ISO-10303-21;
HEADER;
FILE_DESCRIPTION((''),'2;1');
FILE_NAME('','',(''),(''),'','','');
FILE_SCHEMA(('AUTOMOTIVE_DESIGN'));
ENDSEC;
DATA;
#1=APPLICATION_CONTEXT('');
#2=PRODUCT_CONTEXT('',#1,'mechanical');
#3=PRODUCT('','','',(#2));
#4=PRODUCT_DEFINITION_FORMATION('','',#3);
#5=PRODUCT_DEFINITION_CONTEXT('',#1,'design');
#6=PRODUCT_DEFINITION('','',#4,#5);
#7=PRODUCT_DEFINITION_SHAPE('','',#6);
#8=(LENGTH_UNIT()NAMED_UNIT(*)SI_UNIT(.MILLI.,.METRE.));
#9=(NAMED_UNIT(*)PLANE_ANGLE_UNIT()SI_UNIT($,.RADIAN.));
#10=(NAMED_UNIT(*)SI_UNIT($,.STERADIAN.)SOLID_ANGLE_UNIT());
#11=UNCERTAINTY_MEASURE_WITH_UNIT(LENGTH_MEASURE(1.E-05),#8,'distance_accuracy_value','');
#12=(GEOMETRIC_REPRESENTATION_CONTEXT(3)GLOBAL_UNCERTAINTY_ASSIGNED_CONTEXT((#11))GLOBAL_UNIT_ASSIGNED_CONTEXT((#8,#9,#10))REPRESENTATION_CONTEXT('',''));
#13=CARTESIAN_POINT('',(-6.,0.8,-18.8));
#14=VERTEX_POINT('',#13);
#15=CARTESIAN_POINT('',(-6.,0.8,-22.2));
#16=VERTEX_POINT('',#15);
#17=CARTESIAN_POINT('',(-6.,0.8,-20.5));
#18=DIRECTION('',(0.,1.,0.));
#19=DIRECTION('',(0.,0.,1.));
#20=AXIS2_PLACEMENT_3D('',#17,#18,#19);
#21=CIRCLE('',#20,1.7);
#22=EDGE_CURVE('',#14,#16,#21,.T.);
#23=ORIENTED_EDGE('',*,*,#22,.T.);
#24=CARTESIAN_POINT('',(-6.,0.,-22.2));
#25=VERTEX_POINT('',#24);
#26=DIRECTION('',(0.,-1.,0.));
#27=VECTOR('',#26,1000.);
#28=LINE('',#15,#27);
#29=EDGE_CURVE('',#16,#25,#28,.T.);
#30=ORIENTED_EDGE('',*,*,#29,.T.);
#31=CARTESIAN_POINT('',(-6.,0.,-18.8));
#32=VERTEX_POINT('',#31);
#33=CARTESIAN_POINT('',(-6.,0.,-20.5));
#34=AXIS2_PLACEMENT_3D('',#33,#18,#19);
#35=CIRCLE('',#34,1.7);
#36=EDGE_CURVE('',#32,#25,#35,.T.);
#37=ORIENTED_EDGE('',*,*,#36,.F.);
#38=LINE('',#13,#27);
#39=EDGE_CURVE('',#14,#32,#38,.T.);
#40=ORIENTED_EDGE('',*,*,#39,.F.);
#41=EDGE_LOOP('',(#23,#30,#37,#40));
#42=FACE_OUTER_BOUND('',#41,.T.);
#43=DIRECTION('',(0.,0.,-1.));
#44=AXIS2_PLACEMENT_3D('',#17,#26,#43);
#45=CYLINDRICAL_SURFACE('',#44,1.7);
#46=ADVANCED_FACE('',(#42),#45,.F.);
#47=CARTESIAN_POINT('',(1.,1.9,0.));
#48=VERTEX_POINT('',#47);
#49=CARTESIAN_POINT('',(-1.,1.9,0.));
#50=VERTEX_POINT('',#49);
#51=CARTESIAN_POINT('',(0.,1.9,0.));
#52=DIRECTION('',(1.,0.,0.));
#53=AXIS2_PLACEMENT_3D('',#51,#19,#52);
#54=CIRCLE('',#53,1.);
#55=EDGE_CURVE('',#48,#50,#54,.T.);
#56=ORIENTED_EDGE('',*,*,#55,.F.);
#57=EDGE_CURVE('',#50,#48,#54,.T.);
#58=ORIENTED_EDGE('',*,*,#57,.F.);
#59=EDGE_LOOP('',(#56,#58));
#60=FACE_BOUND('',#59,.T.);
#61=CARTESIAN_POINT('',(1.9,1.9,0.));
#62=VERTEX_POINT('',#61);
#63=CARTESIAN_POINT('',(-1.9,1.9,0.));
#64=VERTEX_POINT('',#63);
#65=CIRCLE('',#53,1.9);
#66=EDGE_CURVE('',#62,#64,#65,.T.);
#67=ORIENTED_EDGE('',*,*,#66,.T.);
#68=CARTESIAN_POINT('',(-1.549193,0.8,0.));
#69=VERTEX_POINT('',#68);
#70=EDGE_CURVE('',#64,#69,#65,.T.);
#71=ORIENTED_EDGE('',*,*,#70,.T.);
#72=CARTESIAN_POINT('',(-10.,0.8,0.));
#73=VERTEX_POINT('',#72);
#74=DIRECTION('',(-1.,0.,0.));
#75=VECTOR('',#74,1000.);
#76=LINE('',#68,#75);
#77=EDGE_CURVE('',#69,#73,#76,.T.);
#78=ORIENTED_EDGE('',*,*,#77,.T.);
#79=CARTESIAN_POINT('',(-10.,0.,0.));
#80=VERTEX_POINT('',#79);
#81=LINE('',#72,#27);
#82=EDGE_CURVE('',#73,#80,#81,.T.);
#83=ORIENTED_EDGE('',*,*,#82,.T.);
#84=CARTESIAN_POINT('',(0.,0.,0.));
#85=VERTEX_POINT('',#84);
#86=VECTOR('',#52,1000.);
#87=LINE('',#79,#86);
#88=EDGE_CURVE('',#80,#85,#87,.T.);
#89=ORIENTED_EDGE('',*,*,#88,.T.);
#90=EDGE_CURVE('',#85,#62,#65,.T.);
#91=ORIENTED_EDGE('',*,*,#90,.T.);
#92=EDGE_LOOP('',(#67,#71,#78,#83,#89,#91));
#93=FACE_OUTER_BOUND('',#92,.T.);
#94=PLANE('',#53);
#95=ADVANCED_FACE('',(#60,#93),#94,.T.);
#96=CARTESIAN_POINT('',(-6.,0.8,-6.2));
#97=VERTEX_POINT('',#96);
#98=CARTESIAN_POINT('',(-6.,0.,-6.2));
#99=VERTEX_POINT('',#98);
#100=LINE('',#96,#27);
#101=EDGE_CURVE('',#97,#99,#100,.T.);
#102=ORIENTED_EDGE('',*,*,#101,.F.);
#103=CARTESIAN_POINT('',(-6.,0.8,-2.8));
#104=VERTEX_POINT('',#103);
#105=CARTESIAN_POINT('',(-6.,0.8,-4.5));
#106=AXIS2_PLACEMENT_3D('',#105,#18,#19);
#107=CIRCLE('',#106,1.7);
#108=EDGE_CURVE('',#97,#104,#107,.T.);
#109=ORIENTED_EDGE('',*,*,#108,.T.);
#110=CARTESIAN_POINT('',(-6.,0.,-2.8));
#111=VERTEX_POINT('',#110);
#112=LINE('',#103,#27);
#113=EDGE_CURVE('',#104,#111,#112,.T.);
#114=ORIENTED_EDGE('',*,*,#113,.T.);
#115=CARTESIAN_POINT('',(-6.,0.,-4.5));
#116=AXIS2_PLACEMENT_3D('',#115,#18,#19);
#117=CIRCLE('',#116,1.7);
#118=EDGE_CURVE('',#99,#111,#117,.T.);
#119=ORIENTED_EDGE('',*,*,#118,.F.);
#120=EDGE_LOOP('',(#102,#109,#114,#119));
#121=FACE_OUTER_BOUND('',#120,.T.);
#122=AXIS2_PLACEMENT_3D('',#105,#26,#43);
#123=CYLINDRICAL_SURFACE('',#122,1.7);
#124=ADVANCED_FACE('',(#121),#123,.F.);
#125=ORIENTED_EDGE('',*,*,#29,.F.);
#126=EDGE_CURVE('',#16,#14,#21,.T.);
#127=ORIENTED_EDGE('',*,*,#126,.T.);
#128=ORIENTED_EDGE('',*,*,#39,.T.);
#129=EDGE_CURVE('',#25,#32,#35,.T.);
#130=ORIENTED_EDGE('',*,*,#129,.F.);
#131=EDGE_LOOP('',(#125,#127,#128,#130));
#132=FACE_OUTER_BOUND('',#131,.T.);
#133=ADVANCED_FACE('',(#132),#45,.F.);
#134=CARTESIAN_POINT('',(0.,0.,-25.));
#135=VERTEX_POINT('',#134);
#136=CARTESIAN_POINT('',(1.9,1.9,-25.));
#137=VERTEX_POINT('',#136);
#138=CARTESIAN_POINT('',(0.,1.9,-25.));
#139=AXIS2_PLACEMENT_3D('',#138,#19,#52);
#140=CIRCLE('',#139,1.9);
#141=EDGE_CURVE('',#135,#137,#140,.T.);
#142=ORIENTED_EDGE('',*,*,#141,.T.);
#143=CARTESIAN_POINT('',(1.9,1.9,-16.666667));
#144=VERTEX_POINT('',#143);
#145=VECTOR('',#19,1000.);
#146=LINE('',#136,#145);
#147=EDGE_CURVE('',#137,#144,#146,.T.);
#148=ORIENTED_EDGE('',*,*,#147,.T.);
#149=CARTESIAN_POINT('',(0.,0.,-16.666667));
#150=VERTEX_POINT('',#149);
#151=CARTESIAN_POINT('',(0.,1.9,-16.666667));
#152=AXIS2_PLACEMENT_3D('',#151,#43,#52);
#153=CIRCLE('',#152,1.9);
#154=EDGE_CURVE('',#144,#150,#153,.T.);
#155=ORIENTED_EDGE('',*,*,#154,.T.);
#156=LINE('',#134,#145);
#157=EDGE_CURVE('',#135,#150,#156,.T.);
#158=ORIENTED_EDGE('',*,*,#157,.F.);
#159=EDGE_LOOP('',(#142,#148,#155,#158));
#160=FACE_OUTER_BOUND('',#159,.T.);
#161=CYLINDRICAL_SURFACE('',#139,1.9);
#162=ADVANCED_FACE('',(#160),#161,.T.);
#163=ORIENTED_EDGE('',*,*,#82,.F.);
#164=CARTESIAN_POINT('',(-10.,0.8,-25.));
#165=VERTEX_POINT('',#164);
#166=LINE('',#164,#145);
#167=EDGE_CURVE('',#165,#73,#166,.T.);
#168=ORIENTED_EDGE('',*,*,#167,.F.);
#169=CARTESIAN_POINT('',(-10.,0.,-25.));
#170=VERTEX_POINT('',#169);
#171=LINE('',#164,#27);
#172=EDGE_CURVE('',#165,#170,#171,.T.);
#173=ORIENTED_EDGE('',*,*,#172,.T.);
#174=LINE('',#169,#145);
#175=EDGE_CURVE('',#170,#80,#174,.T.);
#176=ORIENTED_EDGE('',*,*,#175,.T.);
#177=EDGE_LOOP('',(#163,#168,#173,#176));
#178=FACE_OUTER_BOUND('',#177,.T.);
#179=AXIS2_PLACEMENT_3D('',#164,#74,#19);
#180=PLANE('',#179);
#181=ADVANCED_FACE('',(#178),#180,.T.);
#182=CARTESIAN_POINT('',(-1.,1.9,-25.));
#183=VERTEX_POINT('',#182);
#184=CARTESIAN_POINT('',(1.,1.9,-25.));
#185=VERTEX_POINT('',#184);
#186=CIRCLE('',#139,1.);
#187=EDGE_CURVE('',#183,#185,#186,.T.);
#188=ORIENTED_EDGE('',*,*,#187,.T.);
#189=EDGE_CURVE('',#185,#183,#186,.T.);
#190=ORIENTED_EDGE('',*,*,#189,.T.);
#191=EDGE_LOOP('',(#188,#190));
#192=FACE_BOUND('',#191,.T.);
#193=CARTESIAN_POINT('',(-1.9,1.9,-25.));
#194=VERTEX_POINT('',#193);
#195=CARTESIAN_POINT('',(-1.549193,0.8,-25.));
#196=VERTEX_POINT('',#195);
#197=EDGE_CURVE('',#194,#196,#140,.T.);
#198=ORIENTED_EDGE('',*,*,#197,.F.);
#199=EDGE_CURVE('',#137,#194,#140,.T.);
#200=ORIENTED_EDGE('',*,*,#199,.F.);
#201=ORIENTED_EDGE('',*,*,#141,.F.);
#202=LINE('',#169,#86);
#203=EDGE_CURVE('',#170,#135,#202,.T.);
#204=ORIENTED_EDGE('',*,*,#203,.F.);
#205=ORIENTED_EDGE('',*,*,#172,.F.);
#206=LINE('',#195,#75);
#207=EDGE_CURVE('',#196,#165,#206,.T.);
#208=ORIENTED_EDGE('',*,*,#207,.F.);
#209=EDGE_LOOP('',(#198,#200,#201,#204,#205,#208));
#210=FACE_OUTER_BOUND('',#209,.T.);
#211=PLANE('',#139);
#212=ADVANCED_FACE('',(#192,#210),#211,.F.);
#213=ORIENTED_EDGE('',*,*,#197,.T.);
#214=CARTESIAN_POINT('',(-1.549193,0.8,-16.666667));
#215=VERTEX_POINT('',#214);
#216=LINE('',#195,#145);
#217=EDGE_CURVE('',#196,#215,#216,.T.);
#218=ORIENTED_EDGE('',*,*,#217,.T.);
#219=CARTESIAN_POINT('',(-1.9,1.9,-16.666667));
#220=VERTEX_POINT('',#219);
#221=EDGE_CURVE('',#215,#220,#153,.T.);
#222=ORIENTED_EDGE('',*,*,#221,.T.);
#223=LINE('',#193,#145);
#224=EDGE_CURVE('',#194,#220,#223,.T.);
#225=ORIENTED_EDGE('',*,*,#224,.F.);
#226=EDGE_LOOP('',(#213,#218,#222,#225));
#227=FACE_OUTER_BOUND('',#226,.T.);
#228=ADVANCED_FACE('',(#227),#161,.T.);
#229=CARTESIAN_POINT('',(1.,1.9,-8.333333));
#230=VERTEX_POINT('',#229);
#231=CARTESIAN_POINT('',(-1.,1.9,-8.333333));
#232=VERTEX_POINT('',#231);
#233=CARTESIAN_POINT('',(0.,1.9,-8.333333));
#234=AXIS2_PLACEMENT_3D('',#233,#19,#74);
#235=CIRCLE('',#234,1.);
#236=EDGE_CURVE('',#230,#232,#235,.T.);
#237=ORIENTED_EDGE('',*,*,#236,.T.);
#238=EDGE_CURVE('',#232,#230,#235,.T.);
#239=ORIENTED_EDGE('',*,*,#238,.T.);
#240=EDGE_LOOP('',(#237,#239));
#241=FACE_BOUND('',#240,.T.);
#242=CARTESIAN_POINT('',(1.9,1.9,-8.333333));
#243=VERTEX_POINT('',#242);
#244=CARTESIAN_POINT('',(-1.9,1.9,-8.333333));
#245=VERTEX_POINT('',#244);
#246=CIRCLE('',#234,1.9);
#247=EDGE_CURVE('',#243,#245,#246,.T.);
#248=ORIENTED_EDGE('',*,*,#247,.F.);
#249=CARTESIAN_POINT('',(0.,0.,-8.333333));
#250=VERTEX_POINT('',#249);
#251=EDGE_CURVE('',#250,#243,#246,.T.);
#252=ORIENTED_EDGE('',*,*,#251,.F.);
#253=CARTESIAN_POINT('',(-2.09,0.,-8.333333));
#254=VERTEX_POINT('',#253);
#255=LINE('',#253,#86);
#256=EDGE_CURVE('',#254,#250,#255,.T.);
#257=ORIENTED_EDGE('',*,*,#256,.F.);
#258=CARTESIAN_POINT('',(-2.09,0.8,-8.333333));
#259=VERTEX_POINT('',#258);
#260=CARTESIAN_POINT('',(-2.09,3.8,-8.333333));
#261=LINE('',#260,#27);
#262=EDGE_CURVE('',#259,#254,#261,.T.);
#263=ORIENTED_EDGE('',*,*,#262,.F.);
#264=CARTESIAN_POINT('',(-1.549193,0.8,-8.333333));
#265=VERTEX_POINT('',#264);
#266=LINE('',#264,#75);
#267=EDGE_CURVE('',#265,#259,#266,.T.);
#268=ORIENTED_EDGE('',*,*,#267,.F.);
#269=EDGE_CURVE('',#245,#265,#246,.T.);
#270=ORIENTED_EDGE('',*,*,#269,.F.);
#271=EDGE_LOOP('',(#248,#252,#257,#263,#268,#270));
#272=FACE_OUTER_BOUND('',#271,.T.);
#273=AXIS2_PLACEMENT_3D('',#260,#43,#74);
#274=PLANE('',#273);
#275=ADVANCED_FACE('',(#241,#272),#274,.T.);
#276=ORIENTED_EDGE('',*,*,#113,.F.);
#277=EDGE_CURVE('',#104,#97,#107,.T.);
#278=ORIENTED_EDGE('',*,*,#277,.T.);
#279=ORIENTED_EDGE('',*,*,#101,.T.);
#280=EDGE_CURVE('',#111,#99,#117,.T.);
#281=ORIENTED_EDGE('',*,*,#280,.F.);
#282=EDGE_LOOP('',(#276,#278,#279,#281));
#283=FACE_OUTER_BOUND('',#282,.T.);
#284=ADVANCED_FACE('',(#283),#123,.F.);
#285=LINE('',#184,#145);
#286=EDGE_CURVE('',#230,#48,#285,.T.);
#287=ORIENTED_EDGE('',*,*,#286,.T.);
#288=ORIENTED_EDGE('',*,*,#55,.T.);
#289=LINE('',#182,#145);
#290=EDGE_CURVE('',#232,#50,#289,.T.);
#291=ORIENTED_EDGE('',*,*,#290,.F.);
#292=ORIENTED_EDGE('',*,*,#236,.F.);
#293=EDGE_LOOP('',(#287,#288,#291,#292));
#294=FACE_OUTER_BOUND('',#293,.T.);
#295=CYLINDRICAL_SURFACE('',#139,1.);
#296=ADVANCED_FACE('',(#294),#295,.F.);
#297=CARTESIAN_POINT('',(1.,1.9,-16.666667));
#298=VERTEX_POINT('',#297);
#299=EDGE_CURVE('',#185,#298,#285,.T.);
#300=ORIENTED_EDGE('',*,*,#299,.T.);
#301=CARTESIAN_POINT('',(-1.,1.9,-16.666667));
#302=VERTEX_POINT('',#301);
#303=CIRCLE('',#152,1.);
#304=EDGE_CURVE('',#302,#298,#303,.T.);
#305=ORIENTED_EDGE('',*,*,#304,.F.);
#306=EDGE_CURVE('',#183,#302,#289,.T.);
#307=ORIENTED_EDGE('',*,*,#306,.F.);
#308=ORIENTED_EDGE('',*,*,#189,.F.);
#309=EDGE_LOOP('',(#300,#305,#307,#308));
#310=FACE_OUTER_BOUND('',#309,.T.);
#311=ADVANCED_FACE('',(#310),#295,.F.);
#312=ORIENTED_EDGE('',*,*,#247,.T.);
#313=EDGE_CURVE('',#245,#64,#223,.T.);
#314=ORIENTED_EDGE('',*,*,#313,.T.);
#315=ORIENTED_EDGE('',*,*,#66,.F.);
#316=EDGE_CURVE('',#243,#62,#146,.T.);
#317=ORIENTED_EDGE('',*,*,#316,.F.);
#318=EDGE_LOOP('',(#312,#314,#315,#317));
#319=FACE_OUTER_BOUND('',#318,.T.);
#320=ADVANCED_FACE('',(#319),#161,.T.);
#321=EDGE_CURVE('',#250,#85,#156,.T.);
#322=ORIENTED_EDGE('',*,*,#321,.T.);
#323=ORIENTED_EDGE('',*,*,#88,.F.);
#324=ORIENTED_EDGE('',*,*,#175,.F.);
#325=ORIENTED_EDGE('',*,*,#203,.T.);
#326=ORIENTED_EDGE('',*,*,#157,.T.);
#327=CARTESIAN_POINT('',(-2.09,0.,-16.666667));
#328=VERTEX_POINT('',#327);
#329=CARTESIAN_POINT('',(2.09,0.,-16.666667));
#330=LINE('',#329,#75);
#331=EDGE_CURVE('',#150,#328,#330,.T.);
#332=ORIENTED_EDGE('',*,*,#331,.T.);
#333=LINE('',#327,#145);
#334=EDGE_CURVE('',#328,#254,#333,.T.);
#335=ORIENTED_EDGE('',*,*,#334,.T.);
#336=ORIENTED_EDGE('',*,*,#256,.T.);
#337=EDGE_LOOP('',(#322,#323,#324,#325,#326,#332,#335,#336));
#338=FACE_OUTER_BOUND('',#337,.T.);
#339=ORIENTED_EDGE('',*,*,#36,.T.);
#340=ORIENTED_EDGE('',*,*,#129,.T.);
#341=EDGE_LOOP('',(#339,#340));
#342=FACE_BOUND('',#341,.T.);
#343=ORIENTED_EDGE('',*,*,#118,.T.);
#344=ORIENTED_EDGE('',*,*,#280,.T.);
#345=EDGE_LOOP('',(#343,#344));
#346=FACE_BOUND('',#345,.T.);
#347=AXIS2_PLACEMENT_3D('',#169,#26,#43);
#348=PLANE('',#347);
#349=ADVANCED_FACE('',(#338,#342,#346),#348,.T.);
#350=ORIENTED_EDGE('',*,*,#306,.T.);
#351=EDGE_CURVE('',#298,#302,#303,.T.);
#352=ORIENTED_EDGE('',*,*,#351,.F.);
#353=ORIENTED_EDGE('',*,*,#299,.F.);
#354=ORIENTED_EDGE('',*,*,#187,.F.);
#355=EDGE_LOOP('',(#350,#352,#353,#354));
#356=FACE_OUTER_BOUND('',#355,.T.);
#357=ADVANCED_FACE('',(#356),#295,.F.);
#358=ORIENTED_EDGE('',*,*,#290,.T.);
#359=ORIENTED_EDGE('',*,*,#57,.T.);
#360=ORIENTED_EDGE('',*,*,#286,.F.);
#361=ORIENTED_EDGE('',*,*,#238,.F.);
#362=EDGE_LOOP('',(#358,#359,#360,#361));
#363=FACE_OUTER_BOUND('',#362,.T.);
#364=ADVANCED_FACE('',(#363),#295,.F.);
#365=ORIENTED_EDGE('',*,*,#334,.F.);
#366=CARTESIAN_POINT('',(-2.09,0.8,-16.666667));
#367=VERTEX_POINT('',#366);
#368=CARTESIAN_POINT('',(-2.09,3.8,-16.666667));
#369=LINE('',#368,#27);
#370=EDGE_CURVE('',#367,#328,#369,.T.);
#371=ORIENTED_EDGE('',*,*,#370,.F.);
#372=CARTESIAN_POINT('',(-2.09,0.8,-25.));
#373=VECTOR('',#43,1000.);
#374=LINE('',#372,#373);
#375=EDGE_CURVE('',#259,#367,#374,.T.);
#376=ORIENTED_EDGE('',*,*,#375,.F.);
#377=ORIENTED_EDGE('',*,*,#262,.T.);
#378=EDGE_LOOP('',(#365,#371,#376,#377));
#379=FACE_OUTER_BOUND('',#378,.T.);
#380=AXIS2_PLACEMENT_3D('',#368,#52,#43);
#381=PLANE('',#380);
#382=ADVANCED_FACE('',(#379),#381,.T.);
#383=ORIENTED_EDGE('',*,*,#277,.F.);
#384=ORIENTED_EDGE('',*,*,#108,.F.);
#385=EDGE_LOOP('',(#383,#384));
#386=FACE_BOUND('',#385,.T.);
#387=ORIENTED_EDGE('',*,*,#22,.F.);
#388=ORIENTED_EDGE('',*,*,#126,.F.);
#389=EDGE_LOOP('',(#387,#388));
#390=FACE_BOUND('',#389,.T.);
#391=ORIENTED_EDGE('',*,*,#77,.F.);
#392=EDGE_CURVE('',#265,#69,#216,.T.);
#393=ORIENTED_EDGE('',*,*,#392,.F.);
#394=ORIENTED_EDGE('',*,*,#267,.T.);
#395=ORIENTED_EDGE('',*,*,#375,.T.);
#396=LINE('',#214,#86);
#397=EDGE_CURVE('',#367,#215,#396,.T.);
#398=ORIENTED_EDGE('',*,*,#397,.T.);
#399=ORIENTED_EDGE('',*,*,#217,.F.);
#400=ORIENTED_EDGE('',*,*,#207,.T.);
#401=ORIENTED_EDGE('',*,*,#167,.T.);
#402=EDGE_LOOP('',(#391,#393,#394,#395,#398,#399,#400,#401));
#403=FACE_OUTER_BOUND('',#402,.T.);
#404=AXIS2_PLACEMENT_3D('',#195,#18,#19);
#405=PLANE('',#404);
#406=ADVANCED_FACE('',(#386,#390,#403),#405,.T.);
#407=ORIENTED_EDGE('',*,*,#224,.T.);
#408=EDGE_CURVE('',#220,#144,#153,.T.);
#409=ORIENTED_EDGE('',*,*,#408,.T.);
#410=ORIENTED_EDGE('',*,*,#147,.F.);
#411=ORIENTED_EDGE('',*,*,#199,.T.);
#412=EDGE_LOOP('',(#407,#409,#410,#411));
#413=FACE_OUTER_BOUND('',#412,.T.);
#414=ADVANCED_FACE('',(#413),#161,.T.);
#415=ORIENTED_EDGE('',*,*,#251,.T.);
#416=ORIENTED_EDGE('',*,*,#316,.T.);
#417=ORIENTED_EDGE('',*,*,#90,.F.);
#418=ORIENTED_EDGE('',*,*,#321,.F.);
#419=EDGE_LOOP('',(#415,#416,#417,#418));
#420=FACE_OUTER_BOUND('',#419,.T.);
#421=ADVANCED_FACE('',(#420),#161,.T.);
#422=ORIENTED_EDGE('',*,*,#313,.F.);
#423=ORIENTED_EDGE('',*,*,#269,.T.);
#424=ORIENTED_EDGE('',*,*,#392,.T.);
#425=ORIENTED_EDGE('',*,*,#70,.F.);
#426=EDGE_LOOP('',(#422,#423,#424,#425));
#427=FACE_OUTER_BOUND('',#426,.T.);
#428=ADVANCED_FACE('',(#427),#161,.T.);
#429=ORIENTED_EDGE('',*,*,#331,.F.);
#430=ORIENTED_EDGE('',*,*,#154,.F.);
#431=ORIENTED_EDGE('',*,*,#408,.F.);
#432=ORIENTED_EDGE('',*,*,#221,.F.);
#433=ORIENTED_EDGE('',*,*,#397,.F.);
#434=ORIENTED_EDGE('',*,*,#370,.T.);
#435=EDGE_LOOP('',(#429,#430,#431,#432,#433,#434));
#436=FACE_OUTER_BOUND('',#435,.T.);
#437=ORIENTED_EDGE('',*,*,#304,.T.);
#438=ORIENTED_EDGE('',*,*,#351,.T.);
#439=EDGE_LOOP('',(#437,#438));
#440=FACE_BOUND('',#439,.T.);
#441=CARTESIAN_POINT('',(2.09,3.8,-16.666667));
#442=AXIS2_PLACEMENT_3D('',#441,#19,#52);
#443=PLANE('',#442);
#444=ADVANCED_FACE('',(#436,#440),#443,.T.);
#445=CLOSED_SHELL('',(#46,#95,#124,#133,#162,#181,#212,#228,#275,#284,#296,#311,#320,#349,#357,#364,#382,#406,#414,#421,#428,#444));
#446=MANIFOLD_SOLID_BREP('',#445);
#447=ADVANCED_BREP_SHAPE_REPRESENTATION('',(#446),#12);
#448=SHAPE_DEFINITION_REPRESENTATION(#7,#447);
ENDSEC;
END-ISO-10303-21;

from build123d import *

# Parameters (mm, degrees)
SKETCH_1_R          = 1
EXTRUDE_1_DEPTH     = 25
CUT_EXTRUDE_1_DEPTH = 3.8
SKETCH_3_R          = 1.7
CUT_EXTRUDE_2_DEPTH = 0.8
SKETCH_4_R          = 1.7
CUT_EXTRUDE_3_DEPTH = 0.8


with BuildPart() as part:
    # 草图1 → 凸台-拉伸1 (new body)
    with BuildSketch(Plane.XY):
        with BuildLine():
            Line((-10, 0), (0, 0))
            ThreePointArc((0, 0), (0.871779789, 3.588194302), (-1.549193338, 0.8))
            Line((-1.549193338, 0.8), (-10, 0.8))
            Line((-10, 0.8), (-10, 0))
        make_face()
        with Locations((0, 1.9)):
            Circle(SKETCH_1_R, mode=Mode.SUBTRACT)
    extrude(amount=-EXTRUDE_1_DEPTH)

    # 草图2 → 切除-拉伸1 (cut)
    with BuildSketch(Plane(origin=(0, 0, 0), x_dir=(1, 0, 0), z_dir=(0, 1, 0))):
        Polygon((-2.09, 8.333333333), (2.09, 8.333333333), (2.09, 0), (6, 0), (6, 25), (2.09, 25), (2.09, 16.666666667), (-2.09, 16.666666667), align=None)
    extrude(amount=CUT_EXTRUDE_1_DEPTH, mode=Mode.SUBTRACT)

    # 草图3 → 切除-拉伸2 (cut)
    with BuildSketch(Plane(origin=(0, 0, 0), x_dir=(1, 0, 0), z_dir=(0, 1, 0))):
        with Locations(Location((-6, 20.5, 0), (0, 0, 270))):
            Circle(SKETCH_3_R)
    extrude(amount=CUT_EXTRUDE_2_DEPTH, mode=Mode.SUBTRACT)

    # 草图4 → 切除-拉伸3 (cut)
    with BuildSketch(Plane(origin=(0, 0, 0), x_dir=(1, 0, 0), z_dir=(0, 1, 0))):
        with Locations(Location((-6, 4.5, 0), (0, 0, 270))):
            Circle(SKETCH_4_R)
    extrude(amount=CUT_EXTRUDE_3_DEPTH, mode=Mode.SUBTRACT)


solid = part.part
